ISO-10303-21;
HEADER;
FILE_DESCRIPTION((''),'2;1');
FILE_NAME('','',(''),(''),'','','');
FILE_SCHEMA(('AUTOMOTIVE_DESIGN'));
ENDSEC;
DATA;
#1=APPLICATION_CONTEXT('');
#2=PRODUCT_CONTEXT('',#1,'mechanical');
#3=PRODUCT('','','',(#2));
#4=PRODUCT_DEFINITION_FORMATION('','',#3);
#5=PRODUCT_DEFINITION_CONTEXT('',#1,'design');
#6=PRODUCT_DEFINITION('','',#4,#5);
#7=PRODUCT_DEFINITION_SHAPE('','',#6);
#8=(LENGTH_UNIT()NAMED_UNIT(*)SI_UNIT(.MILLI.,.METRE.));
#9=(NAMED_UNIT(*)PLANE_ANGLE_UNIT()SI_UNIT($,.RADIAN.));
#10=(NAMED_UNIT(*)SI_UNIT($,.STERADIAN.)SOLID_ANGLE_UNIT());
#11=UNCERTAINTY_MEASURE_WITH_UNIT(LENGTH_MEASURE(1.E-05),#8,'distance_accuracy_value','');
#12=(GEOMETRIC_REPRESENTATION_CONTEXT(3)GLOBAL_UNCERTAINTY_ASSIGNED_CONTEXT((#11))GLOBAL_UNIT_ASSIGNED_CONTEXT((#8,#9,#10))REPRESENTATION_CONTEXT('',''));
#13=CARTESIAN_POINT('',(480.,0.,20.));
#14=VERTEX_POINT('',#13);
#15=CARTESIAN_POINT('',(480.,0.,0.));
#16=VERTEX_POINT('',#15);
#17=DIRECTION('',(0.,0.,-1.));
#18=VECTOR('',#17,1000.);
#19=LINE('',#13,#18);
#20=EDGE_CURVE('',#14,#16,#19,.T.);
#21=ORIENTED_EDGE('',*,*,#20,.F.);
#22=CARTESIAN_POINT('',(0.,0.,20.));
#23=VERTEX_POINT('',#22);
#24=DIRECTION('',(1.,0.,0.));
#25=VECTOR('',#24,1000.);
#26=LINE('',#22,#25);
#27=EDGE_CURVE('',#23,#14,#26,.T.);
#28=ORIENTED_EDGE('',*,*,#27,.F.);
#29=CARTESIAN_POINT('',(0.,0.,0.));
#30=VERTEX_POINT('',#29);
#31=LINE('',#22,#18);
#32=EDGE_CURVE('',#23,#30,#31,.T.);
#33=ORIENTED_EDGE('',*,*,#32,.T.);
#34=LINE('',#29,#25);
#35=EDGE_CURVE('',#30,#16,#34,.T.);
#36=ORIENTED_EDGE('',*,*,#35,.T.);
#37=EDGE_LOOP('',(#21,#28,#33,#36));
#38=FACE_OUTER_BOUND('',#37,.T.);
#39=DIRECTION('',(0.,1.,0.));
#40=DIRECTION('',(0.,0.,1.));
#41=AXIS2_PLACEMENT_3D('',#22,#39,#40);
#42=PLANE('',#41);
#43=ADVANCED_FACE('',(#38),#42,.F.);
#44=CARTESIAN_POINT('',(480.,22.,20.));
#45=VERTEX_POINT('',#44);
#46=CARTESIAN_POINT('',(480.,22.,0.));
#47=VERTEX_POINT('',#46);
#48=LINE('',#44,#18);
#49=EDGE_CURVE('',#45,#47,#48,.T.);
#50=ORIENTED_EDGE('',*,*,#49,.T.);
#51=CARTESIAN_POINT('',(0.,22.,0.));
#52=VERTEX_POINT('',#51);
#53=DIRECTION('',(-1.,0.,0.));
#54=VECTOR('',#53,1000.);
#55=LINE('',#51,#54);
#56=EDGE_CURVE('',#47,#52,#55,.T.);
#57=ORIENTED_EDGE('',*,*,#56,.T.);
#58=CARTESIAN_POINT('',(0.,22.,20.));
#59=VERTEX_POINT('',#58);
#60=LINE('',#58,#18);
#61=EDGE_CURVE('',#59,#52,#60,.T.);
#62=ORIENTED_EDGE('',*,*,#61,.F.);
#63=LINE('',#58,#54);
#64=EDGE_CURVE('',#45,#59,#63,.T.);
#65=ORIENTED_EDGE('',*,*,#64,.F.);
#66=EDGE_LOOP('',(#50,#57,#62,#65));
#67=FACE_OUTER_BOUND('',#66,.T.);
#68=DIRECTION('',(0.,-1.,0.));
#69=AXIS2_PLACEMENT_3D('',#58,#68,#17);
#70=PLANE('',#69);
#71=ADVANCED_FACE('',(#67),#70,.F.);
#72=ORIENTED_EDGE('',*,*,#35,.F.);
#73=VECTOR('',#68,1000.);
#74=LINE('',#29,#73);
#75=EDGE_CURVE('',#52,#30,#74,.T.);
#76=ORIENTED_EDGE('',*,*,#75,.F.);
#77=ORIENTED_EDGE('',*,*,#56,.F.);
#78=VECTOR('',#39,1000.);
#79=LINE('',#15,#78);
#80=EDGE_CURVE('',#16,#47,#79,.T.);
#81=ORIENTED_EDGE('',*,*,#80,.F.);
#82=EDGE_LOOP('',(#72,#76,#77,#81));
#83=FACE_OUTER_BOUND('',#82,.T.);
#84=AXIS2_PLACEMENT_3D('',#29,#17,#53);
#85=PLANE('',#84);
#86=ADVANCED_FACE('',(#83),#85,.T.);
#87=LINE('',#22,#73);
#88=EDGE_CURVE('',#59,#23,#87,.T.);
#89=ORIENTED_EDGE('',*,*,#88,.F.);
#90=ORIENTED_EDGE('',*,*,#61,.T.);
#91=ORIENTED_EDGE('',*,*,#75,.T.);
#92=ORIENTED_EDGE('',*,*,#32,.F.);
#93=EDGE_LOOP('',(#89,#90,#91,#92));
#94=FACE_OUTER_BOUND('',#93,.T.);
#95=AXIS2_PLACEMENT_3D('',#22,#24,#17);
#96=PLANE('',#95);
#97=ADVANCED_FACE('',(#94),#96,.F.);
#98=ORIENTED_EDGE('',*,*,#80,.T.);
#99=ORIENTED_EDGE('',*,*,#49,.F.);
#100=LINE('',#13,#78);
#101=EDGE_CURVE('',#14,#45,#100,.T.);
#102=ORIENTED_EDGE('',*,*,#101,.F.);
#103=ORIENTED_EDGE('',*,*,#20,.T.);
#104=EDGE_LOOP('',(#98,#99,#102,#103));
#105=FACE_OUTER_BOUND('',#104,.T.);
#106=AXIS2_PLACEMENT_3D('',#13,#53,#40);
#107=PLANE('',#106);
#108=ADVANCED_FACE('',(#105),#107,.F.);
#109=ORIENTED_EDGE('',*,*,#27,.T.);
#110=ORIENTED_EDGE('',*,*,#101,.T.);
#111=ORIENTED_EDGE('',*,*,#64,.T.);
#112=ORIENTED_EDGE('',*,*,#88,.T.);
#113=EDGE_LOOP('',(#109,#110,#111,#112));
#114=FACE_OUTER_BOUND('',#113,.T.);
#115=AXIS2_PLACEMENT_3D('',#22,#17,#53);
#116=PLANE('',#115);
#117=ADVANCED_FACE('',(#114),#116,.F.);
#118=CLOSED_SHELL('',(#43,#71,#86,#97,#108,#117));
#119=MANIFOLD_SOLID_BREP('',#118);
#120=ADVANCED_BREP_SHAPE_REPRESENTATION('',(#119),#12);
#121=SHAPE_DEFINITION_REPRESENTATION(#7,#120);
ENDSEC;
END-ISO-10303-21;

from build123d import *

# Parameters (mm, degrees)
SKETCH1_W           = 480
SKETCH1_H           = 22
BOSS_EXTRUDE1_DEPTH = 20


with BuildPart() as part:
    # Sketch1 → Boss-Extrude1 (new body)
    with BuildSketch(Plane.XY):
        with Locations((240, 11)):
            Rectangle(SKETCH1_W, SKETCH1_H)
    extrude(amount=BOSS_EXTRUDE1_DEPTH)


solid = part.part
